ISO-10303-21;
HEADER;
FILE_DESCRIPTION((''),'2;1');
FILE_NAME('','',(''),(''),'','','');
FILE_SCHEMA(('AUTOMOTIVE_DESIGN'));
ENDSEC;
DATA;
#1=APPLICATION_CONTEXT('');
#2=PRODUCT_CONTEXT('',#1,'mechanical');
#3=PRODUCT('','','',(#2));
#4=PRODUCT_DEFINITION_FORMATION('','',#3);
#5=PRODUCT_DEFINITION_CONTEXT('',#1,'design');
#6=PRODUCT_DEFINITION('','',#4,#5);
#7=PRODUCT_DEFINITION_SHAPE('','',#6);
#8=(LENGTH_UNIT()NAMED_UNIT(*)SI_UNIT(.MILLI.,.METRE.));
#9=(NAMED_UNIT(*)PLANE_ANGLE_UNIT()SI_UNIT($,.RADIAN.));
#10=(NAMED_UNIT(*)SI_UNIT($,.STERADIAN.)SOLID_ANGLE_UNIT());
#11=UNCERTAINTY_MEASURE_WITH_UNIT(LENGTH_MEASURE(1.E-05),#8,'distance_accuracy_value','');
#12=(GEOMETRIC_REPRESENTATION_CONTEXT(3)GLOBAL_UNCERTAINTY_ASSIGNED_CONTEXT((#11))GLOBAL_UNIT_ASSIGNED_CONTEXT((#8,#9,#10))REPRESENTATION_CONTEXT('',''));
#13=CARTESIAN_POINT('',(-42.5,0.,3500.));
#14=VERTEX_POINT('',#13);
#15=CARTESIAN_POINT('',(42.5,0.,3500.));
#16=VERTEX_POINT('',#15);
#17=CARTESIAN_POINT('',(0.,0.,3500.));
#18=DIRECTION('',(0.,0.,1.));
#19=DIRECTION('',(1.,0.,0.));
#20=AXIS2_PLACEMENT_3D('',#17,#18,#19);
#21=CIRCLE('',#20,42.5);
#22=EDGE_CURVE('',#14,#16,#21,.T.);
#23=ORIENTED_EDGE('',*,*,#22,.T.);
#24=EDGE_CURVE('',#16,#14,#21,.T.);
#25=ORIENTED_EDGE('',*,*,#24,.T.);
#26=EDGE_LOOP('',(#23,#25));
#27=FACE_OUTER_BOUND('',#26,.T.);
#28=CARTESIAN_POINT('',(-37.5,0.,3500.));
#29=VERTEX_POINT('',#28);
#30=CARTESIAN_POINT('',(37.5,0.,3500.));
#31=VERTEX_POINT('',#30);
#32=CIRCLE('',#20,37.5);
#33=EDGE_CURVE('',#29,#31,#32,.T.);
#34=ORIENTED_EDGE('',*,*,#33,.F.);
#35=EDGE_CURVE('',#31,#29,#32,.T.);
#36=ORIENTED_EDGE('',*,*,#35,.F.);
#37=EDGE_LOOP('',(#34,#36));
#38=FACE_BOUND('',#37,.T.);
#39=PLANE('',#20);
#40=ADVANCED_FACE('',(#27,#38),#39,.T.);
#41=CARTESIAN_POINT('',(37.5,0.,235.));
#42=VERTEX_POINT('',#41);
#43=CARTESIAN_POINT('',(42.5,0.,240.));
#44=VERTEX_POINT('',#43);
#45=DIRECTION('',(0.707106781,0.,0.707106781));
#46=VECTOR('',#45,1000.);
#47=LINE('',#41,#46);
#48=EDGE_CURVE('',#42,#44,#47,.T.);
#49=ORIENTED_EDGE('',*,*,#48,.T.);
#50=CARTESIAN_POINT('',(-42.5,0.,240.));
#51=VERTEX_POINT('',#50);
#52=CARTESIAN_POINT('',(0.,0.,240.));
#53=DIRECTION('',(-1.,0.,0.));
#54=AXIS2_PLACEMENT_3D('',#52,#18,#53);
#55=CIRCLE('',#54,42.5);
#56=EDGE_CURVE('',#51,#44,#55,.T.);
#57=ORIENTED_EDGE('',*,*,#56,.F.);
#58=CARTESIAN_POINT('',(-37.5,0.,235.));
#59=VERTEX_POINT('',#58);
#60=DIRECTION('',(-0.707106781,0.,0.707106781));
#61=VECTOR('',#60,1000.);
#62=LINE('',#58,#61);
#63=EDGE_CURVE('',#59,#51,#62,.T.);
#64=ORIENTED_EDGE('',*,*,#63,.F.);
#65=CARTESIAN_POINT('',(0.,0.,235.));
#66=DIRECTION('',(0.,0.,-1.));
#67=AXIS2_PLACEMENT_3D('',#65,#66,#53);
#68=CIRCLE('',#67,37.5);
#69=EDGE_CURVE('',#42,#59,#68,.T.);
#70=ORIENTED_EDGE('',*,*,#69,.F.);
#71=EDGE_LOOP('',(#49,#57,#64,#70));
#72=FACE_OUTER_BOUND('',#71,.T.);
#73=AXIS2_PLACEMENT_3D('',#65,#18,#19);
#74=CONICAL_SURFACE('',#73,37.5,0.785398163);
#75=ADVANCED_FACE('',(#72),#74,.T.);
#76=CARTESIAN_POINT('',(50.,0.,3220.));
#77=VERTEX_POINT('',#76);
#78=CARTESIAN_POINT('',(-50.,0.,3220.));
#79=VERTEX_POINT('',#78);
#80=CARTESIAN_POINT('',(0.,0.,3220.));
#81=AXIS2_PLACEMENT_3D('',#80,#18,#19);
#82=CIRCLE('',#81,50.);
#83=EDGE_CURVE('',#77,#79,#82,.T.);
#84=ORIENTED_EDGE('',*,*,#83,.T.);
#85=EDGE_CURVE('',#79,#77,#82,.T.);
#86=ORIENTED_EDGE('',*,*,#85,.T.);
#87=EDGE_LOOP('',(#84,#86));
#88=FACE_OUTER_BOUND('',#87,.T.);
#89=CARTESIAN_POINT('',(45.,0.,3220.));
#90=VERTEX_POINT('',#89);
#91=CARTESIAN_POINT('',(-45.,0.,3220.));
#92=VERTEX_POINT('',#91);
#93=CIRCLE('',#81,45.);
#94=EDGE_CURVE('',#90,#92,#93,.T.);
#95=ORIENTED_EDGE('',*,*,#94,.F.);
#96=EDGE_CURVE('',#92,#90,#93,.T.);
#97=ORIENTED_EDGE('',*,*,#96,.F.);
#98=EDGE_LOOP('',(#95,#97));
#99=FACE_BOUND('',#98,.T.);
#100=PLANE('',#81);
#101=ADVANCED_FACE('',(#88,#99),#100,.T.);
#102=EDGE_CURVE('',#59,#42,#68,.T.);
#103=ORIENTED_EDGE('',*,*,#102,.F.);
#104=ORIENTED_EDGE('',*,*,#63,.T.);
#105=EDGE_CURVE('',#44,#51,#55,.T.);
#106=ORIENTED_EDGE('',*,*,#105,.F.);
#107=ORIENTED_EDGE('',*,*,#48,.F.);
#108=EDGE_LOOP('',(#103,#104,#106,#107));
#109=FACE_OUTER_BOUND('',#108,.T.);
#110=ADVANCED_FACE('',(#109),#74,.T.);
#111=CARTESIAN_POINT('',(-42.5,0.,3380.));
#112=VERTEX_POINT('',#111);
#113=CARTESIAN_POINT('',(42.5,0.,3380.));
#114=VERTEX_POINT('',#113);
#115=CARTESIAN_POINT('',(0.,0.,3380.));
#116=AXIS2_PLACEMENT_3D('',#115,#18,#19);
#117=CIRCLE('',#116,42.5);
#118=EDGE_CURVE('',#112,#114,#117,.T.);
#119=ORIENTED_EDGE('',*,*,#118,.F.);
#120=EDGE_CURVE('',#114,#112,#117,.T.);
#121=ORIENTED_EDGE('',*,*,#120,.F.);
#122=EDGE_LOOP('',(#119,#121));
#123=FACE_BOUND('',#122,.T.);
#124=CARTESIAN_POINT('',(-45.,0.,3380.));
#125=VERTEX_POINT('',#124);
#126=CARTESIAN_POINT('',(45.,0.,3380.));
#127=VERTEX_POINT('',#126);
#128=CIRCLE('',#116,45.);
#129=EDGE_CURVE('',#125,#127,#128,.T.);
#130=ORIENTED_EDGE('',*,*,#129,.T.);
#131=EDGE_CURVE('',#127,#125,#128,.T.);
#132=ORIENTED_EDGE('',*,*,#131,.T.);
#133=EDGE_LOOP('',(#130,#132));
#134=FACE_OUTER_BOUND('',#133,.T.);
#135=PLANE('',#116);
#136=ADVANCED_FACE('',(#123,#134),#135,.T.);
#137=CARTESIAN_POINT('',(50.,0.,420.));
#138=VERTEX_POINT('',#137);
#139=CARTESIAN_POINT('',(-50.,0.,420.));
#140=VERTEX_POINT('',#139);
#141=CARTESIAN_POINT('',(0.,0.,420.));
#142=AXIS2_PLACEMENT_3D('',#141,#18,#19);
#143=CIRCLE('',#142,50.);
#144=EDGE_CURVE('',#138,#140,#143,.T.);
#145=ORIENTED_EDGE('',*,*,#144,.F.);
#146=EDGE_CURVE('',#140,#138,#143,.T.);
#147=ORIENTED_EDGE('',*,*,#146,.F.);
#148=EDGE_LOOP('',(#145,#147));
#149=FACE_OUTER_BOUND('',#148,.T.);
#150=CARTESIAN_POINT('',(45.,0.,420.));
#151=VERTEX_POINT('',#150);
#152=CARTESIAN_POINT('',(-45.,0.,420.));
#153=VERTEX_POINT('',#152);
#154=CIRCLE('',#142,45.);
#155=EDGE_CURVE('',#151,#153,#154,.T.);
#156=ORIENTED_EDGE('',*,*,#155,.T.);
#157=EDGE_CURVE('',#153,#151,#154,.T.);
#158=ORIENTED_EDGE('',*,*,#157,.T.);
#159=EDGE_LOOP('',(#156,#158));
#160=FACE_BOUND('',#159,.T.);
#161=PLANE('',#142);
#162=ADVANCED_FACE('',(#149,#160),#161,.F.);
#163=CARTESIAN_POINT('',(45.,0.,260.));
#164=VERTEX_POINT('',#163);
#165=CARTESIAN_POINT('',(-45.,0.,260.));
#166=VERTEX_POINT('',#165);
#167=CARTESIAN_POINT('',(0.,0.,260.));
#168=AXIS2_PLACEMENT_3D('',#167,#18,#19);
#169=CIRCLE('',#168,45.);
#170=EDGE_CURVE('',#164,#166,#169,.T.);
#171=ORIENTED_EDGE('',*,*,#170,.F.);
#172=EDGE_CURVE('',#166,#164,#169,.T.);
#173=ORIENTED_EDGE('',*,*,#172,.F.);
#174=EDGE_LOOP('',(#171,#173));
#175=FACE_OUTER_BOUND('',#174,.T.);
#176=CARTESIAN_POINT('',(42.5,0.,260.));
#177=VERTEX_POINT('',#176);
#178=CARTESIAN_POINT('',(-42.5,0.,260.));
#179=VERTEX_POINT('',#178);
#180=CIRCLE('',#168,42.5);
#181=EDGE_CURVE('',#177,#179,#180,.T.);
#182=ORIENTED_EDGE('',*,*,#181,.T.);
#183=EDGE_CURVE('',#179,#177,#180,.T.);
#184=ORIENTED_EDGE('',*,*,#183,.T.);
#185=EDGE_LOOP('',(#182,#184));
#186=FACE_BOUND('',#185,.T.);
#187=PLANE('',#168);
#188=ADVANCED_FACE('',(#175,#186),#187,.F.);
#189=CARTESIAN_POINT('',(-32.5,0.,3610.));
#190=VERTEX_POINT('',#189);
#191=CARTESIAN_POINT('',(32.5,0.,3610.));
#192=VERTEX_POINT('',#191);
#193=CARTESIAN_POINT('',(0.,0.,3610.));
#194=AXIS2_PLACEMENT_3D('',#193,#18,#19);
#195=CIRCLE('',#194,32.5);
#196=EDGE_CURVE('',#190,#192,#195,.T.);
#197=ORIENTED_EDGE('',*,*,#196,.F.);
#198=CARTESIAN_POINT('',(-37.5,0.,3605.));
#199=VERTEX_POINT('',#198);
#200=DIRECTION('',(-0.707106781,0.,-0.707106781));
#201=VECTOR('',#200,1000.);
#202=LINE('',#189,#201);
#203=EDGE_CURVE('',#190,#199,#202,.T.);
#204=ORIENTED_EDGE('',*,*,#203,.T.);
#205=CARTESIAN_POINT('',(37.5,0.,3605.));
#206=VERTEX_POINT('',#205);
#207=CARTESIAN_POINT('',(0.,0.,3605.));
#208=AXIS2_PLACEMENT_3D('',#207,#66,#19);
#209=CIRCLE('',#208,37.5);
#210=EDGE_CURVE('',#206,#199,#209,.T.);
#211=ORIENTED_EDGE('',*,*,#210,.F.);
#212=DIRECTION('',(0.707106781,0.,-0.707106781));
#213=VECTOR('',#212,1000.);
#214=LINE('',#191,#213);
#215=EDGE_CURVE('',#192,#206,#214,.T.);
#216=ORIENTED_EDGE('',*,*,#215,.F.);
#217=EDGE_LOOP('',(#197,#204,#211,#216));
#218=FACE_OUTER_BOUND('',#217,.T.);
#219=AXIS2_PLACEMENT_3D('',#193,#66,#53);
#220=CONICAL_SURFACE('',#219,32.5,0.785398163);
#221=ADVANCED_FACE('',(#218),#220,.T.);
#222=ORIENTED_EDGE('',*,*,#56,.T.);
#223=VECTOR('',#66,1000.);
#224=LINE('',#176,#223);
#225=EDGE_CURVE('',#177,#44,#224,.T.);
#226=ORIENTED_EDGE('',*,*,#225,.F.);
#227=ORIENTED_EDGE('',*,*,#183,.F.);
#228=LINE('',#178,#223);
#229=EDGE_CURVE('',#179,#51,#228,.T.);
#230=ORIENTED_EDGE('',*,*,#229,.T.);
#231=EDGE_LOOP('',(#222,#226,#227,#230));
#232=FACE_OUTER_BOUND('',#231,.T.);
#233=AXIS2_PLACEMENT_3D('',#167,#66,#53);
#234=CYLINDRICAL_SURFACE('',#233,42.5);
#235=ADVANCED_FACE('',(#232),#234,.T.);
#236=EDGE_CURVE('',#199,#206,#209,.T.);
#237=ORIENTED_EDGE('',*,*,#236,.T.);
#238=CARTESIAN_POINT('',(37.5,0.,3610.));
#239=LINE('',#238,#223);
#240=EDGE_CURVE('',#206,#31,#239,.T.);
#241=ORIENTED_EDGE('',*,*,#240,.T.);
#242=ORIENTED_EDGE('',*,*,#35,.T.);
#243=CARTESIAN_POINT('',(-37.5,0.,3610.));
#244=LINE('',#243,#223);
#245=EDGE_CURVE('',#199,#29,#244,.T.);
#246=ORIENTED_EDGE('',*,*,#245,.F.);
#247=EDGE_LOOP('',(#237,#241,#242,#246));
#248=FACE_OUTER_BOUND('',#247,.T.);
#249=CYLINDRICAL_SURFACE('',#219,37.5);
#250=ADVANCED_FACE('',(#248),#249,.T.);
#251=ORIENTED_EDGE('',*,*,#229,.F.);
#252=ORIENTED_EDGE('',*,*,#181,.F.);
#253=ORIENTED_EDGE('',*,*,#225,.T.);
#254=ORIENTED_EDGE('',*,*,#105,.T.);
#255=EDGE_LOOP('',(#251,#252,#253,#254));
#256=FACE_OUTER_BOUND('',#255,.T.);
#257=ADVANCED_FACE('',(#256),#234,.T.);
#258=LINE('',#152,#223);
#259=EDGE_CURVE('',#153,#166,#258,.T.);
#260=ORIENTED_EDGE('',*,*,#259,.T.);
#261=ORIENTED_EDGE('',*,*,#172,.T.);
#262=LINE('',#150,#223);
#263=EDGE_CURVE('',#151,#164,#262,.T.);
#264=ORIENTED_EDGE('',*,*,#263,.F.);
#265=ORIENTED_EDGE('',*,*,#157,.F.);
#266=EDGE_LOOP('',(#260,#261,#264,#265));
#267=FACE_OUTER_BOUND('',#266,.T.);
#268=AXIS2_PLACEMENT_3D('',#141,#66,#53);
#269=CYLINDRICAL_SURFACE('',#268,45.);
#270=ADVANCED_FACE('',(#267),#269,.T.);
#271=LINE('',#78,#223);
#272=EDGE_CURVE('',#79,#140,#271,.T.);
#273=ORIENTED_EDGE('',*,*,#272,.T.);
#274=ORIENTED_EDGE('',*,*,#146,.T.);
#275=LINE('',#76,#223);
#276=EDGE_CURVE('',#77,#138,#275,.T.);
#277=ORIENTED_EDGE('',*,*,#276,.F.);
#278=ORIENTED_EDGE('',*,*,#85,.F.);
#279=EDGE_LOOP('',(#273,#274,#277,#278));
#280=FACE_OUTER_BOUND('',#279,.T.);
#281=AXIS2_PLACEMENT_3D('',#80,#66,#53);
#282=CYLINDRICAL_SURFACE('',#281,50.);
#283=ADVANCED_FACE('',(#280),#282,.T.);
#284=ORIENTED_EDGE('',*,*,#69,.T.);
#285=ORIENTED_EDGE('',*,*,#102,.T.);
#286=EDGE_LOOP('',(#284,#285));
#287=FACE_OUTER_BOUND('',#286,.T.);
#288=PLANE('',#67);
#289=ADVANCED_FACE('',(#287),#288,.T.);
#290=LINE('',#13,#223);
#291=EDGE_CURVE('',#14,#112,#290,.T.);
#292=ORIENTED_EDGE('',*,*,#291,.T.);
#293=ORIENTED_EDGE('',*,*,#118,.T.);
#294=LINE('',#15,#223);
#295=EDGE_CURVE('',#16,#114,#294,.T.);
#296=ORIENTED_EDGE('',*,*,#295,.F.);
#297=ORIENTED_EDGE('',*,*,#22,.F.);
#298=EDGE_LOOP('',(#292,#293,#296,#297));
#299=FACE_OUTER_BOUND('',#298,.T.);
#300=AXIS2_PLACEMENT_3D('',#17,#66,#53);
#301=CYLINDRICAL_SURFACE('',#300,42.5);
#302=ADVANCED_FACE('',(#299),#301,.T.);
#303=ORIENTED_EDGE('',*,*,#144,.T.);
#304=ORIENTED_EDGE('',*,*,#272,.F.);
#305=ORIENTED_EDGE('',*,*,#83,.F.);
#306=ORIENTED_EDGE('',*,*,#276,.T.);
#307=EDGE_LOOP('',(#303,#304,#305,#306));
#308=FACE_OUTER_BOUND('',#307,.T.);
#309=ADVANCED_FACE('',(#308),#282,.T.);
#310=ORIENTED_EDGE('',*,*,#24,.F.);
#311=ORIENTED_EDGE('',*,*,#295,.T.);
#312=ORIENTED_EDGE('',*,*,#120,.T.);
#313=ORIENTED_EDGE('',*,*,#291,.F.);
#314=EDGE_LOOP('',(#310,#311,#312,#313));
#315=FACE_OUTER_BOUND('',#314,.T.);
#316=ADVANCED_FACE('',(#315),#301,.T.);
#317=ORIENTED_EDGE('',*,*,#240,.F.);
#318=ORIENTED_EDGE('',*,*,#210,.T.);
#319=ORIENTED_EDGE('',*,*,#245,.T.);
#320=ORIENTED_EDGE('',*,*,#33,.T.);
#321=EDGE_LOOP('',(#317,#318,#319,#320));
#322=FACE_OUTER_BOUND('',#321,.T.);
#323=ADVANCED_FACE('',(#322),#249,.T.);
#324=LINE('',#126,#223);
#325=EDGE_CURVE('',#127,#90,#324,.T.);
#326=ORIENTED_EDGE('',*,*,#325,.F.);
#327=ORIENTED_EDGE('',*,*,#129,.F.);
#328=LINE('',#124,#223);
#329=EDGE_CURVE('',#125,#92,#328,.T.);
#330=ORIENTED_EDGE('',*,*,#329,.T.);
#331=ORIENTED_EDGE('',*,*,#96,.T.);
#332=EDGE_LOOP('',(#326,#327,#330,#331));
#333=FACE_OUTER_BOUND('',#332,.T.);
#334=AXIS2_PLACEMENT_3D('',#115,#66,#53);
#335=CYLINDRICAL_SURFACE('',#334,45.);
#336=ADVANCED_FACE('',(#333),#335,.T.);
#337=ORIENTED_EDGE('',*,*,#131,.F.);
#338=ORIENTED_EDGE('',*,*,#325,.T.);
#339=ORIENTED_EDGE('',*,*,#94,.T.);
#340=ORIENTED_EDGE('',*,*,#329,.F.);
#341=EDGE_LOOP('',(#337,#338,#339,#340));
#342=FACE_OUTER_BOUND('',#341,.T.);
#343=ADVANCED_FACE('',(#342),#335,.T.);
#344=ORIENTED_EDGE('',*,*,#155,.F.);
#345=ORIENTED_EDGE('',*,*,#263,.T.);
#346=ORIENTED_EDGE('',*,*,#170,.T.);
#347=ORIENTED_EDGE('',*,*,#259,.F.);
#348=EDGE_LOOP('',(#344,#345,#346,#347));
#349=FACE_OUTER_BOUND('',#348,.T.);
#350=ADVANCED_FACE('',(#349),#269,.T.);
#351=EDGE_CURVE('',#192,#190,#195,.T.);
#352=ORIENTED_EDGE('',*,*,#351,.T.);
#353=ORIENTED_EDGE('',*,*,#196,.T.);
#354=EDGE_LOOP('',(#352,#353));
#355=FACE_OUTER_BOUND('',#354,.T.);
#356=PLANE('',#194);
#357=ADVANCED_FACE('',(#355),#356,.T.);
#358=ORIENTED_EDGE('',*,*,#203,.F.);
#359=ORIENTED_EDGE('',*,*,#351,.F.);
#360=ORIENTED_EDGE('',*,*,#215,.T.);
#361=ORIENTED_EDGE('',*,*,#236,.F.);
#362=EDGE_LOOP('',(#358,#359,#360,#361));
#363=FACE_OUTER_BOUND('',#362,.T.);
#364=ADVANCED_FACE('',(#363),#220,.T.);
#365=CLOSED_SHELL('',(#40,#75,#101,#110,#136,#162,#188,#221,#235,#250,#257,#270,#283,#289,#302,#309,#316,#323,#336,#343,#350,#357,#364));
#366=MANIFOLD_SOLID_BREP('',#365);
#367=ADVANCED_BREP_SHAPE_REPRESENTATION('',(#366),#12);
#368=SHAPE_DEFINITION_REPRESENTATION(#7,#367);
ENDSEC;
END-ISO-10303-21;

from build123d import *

# Parameters (mm, degrees)
SKETCH_1_R          = 37.5
EXTRUDE_1_DEPTH     = 140
SKETCH_2_R          = 42.5
EXTRUDE_2_DEPTH     = 120
SKETCH_3_R          = 45
EXTRUDE_3_DEPTH     = 160
SKETCH_4_R          = 50
EXTRUDE_4_DEPTH     = 2800
SKETCH_5_R          = 45
EXTRUDE_5_DEPTH     = 160
SKETCH_6_R          = 42.5
EXTRUDE_6_DEPTH     = 120
SKETCH_7_R          = 37.5
EXTRUDE_7_DEPTH     = 110
SKETCH_8_R          = 75
CUT_EXTRUDE_1_DEPTH = 235
CHAMFER_1_SIZE      = 5


with BuildPart() as part:
    # 草图1 → 凸台-拉伸1 (new body)
    with BuildSketch(Plane.XY):
        Circle(SKETCH_1_R)
    extrude(amount=EXTRUDE_1_DEPTH)

    # 草图2 → 凸台-拉伸2 (add)
    with BuildSketch(Plane.XY.offset(140)):
        Circle(SKETCH_2_R)
    extrude(amount=EXTRUDE_2_DEPTH)

    # 草图3 → 凸台-拉伸3 (add)
    with BuildSketch(Plane.XY.offset(260)):
        Circle(SKETCH_3_R)
    extrude(amount=EXTRUDE_3_DEPTH)

    # 草图4 → 凸台-拉伸4 (add)
    with BuildSketch(Plane.XY.offset(420)):
        Circle(SKETCH_4_R)
    extrude(amount=EXTRUDE_4_DEPTH)

    # 草图5 → 凸台-拉伸5 (add)
    with BuildSketch(Plane.XY.offset(3220)):
        Circle(SKETCH_5_R)
    extrude(amount=EXTRUDE_5_DEPTH)

    # 草图6 → 凸台-拉伸6 (add)
    with BuildSketch(Plane.XY.offset(3380)):
        Circle(SKETCH_6_R)
    extrude(amount=EXTRUDE_6_DEPTH)

    # 草图7 → 凸台-拉伸7 (add)
    with BuildSketch(Plane.XY.offset(3500)):
        Circle(SKETCH_7_R)
    extrude(amount=EXTRUDE_7_DEPTH)

    # 草图8 → 切除-拉伸1 (cut)
    with BuildSketch(Plane(origin=(0, 0, 0), x_dir=(-1, 0, 0), z_dir=(0, 0, -1))):
        Circle(SKETCH_8_R)
    extrude(amount=-CUT_EXTRUDE_1_DEPTH, mode=Mode.SUBTRACT)

    # 倒角1
    chamfer_1_edges = [part.edges().sort_by_distance(p)[0] for p in [
        (-37.5, 0, 3610),
        (-42.5, 0, 235),
    ]]
    chamfer(chamfer_1_edges, length=CHAMFER_1_SIZE)


solid = part.part
